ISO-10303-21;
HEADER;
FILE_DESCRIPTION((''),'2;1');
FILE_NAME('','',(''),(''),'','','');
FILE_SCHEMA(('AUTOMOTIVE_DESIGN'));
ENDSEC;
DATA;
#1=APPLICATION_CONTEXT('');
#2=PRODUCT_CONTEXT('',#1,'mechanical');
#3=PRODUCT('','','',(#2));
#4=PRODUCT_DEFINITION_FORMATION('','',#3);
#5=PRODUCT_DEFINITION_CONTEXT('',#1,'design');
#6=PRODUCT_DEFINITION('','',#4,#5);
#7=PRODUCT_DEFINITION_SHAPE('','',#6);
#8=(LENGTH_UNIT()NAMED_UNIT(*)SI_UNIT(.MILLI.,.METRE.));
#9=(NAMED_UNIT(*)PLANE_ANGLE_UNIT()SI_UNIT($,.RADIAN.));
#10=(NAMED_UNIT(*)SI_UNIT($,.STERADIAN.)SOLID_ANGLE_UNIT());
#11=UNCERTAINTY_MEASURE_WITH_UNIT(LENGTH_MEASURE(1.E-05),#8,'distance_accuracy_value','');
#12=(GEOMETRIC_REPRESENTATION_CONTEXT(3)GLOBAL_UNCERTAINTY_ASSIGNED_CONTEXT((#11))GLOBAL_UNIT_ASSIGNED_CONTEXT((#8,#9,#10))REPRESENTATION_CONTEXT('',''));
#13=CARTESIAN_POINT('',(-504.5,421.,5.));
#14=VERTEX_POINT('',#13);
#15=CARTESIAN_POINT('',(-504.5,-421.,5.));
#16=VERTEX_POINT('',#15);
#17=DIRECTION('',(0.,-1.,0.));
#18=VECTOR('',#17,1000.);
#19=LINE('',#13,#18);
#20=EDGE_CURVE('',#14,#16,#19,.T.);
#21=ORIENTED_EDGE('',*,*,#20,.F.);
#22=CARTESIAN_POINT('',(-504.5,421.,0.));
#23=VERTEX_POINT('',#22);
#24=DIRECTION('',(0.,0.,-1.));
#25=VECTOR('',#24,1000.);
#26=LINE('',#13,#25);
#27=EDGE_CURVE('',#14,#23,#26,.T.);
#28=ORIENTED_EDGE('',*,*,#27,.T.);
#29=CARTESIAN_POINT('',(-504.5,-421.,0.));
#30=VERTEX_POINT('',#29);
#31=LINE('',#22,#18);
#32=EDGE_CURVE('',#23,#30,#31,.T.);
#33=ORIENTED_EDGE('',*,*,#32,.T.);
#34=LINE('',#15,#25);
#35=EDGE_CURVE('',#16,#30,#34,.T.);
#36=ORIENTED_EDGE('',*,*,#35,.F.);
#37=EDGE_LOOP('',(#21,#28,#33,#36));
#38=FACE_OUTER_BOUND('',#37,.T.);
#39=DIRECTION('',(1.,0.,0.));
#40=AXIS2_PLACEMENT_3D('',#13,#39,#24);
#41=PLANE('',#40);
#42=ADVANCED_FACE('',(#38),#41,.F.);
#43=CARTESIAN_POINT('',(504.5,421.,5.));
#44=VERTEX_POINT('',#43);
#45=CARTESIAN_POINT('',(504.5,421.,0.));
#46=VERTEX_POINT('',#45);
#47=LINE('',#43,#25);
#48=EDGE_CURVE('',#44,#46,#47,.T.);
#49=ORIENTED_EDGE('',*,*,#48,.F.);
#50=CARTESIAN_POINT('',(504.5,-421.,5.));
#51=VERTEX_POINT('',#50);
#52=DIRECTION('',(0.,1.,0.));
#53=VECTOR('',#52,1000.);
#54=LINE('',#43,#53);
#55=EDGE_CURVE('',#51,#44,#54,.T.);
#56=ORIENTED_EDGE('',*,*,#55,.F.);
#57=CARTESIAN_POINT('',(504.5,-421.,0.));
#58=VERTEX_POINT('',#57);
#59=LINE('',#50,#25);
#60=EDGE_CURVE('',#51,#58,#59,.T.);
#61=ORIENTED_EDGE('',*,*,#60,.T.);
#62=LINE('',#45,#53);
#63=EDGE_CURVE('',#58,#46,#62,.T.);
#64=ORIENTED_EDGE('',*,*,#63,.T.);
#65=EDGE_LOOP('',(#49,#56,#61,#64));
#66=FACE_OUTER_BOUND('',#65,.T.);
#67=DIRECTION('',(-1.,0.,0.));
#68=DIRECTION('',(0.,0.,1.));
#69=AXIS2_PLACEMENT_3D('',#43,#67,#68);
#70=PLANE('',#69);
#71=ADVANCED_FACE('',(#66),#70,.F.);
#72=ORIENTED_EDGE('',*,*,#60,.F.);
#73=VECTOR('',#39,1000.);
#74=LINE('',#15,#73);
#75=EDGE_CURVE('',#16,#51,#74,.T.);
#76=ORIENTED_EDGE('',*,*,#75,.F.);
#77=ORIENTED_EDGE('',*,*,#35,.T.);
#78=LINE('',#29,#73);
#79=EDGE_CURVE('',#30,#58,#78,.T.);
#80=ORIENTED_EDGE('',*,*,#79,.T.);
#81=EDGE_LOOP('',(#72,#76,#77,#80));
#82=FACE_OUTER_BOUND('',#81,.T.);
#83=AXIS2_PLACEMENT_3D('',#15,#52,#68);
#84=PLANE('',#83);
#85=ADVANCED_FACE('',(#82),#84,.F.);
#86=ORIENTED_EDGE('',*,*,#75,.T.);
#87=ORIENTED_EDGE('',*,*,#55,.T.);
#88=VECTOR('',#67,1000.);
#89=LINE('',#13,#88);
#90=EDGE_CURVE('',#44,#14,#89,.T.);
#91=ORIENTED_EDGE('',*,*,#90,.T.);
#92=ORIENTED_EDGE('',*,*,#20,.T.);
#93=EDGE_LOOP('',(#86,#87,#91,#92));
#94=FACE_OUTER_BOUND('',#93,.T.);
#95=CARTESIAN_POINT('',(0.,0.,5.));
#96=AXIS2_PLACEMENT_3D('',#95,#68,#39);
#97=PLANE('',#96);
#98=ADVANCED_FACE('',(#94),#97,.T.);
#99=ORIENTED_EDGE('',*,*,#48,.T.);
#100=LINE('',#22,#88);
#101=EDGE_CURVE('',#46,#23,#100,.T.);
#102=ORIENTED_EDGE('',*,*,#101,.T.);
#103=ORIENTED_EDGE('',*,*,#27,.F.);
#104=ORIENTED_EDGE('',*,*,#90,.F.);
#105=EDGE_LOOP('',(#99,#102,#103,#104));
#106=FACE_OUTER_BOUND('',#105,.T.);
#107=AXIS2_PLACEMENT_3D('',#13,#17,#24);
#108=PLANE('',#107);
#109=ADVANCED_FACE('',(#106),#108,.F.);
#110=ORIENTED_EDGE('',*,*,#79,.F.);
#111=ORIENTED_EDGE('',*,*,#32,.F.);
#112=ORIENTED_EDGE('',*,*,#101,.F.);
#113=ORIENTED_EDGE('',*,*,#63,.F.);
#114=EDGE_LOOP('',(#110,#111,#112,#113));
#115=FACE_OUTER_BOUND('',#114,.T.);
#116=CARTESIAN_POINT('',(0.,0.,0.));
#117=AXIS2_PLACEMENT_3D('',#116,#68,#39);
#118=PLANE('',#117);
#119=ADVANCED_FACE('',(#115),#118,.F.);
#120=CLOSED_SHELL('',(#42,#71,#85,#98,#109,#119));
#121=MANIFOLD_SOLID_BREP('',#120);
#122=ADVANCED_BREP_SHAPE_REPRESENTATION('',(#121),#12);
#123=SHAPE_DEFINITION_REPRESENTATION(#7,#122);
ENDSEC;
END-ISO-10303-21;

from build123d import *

# Parameters (mm, degrees)
SKETCH_1_W      = 1009
SKETCH_1_H      = 842
EXTRUDE_1_DEPTH = 5


with BuildPart() as part:
    # 草图1 → 凸台-拉伸1 (new body)
    with BuildSketch(Plane.XY):
        Rectangle(SKETCH_1_W, SKETCH_1_H)
    extrude(amount=EXTRUDE_1_DEPTH)


solid = part.part
